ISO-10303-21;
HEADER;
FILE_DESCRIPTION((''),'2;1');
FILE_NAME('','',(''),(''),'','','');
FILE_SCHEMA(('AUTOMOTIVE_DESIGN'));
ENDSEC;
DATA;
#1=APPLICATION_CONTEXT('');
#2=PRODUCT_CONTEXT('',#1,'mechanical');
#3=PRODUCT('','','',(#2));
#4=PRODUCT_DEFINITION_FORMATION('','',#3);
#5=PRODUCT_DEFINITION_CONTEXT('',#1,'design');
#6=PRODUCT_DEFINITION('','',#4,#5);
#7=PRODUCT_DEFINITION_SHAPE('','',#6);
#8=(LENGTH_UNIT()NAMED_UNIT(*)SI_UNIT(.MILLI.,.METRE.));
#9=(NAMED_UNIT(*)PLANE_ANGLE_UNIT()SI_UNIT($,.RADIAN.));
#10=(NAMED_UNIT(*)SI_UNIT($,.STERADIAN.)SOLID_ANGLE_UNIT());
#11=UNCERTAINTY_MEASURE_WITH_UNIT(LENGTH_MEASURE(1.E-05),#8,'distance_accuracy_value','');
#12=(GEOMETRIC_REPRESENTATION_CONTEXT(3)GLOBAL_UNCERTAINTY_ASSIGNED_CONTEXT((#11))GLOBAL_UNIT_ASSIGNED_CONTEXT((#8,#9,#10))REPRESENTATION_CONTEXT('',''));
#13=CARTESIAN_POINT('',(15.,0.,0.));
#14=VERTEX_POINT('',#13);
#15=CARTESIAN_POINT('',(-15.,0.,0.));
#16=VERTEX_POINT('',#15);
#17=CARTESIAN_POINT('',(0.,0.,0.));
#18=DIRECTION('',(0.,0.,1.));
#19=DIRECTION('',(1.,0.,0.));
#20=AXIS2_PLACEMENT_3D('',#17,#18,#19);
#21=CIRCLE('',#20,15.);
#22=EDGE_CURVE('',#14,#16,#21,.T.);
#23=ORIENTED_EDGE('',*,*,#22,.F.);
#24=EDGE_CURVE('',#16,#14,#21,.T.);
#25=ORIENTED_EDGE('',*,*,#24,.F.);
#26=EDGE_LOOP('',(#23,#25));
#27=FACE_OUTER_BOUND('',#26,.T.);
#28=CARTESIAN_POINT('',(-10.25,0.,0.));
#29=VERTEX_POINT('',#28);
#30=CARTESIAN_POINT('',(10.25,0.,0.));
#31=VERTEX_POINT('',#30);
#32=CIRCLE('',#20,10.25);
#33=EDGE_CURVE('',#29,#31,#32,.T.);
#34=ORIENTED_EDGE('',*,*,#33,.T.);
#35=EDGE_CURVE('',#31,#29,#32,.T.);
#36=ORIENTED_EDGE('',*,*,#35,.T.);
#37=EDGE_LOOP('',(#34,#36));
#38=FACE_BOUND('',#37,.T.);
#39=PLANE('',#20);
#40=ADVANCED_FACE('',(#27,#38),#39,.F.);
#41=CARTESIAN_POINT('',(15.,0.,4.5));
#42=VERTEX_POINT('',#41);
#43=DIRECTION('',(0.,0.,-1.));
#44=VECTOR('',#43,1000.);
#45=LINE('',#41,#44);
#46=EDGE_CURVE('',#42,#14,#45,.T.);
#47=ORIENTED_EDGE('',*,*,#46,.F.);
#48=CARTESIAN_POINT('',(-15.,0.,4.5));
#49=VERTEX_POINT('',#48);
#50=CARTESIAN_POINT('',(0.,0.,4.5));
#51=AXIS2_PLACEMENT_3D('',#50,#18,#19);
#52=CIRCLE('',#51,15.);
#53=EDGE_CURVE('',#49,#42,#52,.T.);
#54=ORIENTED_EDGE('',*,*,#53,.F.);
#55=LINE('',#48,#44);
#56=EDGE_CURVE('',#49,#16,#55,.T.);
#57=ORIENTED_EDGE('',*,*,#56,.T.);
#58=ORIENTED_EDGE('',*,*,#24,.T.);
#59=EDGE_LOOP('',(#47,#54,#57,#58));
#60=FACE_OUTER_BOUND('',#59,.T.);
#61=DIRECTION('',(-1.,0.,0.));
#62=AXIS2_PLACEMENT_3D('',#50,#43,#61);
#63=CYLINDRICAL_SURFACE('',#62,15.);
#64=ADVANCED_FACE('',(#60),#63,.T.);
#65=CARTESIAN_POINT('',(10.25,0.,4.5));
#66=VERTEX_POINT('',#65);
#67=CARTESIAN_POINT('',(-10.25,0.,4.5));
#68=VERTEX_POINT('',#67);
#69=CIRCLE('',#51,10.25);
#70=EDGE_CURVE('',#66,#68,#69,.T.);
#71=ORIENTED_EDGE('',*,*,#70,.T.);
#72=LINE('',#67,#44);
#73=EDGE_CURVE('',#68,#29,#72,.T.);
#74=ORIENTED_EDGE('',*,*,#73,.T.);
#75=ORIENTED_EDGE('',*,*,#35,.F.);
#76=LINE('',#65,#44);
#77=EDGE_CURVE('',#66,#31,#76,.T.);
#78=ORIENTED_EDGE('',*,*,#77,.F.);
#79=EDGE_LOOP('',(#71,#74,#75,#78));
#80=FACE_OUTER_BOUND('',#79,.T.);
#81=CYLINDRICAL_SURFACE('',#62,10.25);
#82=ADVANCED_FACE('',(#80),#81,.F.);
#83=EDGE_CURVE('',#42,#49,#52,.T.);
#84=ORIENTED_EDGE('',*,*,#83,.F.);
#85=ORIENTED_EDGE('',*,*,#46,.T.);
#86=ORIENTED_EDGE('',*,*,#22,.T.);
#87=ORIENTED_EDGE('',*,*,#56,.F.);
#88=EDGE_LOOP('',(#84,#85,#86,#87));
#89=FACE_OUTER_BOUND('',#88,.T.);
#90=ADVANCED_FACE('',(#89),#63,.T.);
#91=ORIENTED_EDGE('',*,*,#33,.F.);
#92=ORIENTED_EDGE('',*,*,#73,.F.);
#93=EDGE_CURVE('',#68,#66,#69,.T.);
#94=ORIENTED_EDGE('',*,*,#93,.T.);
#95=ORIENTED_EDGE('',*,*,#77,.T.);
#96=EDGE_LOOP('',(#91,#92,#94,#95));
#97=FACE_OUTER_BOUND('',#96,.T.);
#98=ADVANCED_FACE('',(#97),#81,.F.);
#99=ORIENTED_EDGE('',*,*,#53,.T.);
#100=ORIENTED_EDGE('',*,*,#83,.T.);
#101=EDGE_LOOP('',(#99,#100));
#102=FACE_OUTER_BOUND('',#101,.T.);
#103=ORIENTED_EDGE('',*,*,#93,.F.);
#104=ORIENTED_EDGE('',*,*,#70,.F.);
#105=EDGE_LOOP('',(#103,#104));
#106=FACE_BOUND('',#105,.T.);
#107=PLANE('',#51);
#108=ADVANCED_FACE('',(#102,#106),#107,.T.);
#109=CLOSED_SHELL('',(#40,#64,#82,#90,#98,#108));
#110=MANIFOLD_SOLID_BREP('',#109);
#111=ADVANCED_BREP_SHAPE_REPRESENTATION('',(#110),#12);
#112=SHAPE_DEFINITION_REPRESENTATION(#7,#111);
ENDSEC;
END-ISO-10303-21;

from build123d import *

# Parameters (mm, degrees)
SKETCH_1_R      = 15
SKETCH_1_R_2    = 10.25
EXTRUDE_1_DEPTH = 4.5


with BuildPart() as part:
    # 草图1 → 凸台-拉伸1 (new body)
    with BuildSketch(Plane.XY):
        Circle(SKETCH_1_R)
        Circle(SKETCH_1_R_2, mode=Mode.SUBTRACT)
    extrude(amount=EXTRUDE_1_DEPTH)


solid = part.part
